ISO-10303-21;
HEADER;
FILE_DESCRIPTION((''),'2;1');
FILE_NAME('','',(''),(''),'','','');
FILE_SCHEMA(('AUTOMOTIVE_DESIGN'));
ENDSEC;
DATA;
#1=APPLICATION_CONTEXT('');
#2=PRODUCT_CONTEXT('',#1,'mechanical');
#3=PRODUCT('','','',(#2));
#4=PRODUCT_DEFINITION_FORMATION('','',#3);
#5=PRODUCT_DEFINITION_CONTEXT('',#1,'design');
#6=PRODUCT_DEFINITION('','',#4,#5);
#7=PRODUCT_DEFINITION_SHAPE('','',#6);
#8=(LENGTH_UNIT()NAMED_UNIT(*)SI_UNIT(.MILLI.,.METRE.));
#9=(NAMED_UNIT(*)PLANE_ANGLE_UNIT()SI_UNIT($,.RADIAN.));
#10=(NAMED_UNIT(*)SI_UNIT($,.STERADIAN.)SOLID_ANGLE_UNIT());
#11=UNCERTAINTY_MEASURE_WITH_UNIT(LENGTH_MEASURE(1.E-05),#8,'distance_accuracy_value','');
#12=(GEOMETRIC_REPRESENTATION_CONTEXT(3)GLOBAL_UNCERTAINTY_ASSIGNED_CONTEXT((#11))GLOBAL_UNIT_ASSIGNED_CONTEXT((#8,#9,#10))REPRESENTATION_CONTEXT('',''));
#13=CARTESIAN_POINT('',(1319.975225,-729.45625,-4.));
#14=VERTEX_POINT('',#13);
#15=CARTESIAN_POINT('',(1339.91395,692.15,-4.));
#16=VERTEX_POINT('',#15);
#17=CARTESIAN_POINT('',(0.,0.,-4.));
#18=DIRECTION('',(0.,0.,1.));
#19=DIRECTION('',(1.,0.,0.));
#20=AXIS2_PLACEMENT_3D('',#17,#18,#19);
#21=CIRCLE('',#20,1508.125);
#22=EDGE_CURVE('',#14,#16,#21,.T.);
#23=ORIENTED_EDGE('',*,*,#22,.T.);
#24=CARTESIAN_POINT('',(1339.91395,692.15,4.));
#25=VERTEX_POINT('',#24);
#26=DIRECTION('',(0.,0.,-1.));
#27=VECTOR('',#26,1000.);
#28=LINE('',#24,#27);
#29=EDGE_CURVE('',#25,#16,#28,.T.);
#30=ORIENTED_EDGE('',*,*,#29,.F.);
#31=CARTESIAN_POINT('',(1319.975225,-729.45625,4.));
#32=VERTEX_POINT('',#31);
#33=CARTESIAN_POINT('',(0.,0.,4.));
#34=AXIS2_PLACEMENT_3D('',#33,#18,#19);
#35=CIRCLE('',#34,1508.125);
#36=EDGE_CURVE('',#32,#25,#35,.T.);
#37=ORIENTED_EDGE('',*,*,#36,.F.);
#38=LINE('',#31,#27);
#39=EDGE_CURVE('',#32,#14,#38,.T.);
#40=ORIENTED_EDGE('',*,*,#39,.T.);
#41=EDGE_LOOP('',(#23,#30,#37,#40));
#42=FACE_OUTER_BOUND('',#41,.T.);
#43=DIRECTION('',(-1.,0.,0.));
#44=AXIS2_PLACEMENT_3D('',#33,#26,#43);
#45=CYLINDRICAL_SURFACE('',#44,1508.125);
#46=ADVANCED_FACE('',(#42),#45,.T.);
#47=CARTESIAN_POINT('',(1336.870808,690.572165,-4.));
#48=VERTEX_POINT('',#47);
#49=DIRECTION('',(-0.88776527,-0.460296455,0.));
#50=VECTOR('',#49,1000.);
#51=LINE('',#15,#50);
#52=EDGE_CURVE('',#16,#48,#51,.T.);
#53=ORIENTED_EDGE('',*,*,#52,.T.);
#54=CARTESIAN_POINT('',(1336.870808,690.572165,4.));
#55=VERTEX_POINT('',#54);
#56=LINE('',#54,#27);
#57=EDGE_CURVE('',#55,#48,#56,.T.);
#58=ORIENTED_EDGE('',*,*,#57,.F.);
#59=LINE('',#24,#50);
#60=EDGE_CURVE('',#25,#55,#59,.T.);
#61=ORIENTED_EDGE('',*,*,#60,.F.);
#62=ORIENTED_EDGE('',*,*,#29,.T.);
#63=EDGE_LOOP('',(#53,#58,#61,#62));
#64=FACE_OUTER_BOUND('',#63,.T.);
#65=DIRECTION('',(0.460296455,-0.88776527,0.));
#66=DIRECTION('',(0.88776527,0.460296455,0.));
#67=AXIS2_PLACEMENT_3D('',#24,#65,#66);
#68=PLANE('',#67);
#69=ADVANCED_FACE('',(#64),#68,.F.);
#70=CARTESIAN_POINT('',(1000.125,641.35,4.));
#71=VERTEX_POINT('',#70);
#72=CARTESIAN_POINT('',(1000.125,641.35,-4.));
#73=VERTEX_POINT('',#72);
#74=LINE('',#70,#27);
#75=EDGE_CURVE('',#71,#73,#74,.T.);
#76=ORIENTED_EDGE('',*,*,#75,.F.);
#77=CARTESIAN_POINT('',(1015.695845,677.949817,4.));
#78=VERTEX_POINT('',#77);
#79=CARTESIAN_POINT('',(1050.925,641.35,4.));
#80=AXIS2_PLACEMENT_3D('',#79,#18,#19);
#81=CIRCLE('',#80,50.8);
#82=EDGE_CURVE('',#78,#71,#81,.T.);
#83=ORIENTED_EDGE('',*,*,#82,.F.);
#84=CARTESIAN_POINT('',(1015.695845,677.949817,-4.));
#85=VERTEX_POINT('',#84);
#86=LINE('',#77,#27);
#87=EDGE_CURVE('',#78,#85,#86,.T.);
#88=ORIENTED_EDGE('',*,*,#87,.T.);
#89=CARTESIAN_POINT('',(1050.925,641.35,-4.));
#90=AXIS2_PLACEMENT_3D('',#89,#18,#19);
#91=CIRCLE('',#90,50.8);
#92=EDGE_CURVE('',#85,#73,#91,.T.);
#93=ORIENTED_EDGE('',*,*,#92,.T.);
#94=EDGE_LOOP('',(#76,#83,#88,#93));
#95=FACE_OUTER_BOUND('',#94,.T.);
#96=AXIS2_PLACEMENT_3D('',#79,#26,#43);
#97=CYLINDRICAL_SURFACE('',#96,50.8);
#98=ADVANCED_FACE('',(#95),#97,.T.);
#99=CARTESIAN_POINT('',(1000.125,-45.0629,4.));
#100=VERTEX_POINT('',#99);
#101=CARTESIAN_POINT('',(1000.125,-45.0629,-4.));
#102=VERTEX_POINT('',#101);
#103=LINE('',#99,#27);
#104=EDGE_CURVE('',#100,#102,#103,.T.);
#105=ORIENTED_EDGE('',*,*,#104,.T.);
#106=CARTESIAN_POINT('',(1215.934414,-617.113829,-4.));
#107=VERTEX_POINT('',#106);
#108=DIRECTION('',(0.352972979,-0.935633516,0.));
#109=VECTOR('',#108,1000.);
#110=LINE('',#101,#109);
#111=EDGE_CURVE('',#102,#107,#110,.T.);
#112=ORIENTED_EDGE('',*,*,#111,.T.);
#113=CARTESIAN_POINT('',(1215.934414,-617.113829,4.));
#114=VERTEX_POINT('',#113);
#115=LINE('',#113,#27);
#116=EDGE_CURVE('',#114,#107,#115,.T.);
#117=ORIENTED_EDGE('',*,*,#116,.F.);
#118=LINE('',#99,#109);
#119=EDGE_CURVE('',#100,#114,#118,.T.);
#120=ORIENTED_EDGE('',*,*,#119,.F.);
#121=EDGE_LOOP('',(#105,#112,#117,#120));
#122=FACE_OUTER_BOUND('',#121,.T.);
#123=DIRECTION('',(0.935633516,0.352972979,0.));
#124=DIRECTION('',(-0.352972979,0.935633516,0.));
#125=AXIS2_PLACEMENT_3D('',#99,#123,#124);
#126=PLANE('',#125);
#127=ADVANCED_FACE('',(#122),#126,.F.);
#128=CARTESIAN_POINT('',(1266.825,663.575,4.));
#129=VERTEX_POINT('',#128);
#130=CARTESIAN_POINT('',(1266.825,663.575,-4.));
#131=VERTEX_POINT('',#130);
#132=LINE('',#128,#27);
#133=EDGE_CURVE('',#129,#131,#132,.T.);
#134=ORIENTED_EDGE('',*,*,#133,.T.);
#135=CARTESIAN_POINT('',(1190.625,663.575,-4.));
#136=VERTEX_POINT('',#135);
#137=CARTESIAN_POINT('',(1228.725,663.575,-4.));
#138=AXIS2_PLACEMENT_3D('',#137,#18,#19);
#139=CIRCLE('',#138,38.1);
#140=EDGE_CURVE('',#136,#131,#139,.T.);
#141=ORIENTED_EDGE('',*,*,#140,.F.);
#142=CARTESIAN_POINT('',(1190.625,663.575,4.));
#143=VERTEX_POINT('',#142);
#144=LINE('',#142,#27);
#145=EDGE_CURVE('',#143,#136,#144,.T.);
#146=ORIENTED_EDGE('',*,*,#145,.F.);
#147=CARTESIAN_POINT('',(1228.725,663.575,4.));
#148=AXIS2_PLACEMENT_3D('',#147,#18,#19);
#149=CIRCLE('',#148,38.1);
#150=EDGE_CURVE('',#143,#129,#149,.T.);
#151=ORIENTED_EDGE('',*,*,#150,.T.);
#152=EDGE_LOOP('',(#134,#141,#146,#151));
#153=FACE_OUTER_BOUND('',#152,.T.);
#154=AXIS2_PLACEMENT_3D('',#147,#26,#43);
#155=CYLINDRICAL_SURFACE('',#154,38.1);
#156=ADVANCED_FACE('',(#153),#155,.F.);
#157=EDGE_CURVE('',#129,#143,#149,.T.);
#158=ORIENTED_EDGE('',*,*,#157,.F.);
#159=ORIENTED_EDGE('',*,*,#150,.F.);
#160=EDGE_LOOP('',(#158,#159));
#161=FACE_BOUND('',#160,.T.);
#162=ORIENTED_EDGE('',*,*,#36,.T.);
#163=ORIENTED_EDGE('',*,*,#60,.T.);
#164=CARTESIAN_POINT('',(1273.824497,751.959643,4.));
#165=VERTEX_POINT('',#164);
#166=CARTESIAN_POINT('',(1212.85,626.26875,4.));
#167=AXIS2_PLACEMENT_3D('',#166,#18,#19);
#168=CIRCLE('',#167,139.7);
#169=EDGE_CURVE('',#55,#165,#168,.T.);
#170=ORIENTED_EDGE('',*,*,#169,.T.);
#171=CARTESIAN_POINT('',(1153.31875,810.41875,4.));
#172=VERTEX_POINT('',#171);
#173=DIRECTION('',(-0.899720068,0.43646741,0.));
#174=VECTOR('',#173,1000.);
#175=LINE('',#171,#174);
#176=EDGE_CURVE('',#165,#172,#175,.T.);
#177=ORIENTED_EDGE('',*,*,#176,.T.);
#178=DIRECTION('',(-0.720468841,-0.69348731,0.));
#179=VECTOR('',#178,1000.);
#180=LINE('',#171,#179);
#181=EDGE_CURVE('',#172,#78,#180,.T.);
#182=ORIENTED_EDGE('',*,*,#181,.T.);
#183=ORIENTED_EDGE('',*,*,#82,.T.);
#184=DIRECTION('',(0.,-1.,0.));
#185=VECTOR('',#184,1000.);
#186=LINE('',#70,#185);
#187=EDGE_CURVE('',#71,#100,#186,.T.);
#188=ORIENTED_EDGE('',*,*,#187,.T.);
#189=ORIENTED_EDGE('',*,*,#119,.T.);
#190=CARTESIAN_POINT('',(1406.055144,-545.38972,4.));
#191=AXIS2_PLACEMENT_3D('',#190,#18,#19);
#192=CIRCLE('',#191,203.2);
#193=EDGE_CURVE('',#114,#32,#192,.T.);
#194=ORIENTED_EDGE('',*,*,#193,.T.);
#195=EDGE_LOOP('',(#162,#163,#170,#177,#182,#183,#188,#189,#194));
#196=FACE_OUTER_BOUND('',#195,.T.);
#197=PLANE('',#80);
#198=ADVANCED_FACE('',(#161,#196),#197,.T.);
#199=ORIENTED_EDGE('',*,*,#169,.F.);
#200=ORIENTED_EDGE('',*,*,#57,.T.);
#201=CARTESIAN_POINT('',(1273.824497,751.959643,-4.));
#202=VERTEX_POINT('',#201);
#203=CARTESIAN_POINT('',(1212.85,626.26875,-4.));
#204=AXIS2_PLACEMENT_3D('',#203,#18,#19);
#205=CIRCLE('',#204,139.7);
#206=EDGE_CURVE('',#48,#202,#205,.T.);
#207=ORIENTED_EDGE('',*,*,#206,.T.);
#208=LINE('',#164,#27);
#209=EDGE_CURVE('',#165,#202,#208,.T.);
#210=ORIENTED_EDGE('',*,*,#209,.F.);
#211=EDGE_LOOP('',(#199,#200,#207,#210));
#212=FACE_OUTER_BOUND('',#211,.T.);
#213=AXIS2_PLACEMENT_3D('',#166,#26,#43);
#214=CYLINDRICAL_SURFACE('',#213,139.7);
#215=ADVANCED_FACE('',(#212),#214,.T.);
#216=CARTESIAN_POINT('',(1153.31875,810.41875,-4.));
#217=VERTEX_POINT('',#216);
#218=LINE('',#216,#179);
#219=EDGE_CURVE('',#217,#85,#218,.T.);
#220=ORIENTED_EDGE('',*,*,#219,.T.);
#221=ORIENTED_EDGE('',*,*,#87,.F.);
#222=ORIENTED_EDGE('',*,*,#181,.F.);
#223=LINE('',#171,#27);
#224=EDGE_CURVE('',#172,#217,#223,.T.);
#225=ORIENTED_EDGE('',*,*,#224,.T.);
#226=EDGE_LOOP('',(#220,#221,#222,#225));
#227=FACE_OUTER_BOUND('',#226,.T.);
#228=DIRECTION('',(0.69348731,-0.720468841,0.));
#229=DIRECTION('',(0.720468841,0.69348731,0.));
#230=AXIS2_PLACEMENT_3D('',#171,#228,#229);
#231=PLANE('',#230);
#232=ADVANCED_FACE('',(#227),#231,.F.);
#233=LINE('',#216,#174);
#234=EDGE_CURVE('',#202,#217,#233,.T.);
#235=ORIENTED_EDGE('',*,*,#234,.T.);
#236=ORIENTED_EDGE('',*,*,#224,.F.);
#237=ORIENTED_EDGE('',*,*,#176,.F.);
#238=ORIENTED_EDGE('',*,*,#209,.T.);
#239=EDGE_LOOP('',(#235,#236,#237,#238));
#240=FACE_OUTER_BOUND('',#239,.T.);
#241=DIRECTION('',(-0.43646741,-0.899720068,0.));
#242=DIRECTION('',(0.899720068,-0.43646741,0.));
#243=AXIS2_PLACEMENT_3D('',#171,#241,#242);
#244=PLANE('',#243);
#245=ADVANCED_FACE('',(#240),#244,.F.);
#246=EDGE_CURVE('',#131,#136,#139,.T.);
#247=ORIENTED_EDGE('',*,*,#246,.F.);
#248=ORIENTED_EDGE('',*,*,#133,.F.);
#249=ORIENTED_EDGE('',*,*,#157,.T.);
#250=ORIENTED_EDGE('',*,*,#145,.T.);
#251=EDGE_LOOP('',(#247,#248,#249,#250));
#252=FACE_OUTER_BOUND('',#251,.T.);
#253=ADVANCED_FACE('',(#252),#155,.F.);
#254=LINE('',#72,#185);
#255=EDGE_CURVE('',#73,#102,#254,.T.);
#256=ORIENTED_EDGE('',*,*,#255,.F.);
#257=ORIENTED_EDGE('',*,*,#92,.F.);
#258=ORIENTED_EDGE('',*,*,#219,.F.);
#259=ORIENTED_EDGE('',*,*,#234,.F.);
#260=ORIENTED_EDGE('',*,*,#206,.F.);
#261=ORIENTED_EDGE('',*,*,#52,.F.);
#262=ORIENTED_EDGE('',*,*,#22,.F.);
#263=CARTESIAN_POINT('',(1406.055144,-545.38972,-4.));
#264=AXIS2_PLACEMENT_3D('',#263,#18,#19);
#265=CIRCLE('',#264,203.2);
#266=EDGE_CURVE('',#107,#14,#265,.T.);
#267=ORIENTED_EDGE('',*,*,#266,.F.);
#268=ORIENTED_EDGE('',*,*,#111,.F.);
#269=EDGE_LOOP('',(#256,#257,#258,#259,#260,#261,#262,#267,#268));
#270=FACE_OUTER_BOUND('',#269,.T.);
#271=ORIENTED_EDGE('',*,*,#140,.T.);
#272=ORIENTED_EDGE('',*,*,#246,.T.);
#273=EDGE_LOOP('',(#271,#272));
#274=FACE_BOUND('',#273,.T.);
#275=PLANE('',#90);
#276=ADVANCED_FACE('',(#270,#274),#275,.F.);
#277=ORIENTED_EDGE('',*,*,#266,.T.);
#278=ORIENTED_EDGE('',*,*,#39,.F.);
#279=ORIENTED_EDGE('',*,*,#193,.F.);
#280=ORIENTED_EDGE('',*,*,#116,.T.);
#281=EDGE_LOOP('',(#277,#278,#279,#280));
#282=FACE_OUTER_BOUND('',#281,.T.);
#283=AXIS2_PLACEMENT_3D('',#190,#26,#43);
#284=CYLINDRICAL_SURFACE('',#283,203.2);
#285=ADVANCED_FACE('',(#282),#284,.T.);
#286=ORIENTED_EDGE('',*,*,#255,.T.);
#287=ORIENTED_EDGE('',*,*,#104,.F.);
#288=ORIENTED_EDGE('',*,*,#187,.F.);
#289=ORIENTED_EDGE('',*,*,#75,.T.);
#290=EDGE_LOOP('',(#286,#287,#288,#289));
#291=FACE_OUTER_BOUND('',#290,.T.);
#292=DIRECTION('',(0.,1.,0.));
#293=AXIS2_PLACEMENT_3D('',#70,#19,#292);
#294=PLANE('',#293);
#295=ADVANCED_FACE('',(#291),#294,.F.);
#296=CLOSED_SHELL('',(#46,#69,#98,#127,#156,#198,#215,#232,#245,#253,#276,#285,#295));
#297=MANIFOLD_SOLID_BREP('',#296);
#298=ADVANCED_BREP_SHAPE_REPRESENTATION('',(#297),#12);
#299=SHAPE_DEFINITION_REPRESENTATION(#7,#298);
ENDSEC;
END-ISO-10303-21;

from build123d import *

# Parameters (mm, degrees)
SKETCH1_R           = 38.1
BOSS_EXTRUDE1_DEPTH = 4


with BuildPart() as part:
    # Sketch1 → Boss-Extrude1 (new, symmetric)
    with BuildSketch(Plane.XY):
        with BuildLine():
            Line((1000.125, 641.35), (1000.125, -45.0629))
            Line((1000.125, -45.0629), (1215.934413963, -617.113829271))
            ThreePointArc((1215.934413963, -617.113829271), (1256.96824156, -683.459757951), (1319.975225131, -729.45625))
            ThreePointArc((1319.975225131, -729.45625), (1507.976686944, -21.150112495), (1339.913949896, 692.15))
            Line((1339.913949896, 692.15), (1336.870808151, 690.572164727))
            ThreePointArc((1336.870808151, 690.572164727), (1310.307279769, 726.359551875), (1273.824497124, 751.959643467))
            Line((1273.824497124, 751.959643467), (1153.31875, 810.41875))
            Line((1153.31875, 810.41875), (1015.69584463, 677.949817102))
            ThreePointArc((1015.69584463, 677.949817102), (1004.179513091, 661.237168064), (1000.125, 641.35))
        make_face()
        with Locations((1228.725, 663.575)):
            Circle(SKETCH1_R, mode=Mode.SUBTRACT)
    extrude(amount=BOSS_EXTRUDE1_DEPTH, both=True)


solid = part.part
